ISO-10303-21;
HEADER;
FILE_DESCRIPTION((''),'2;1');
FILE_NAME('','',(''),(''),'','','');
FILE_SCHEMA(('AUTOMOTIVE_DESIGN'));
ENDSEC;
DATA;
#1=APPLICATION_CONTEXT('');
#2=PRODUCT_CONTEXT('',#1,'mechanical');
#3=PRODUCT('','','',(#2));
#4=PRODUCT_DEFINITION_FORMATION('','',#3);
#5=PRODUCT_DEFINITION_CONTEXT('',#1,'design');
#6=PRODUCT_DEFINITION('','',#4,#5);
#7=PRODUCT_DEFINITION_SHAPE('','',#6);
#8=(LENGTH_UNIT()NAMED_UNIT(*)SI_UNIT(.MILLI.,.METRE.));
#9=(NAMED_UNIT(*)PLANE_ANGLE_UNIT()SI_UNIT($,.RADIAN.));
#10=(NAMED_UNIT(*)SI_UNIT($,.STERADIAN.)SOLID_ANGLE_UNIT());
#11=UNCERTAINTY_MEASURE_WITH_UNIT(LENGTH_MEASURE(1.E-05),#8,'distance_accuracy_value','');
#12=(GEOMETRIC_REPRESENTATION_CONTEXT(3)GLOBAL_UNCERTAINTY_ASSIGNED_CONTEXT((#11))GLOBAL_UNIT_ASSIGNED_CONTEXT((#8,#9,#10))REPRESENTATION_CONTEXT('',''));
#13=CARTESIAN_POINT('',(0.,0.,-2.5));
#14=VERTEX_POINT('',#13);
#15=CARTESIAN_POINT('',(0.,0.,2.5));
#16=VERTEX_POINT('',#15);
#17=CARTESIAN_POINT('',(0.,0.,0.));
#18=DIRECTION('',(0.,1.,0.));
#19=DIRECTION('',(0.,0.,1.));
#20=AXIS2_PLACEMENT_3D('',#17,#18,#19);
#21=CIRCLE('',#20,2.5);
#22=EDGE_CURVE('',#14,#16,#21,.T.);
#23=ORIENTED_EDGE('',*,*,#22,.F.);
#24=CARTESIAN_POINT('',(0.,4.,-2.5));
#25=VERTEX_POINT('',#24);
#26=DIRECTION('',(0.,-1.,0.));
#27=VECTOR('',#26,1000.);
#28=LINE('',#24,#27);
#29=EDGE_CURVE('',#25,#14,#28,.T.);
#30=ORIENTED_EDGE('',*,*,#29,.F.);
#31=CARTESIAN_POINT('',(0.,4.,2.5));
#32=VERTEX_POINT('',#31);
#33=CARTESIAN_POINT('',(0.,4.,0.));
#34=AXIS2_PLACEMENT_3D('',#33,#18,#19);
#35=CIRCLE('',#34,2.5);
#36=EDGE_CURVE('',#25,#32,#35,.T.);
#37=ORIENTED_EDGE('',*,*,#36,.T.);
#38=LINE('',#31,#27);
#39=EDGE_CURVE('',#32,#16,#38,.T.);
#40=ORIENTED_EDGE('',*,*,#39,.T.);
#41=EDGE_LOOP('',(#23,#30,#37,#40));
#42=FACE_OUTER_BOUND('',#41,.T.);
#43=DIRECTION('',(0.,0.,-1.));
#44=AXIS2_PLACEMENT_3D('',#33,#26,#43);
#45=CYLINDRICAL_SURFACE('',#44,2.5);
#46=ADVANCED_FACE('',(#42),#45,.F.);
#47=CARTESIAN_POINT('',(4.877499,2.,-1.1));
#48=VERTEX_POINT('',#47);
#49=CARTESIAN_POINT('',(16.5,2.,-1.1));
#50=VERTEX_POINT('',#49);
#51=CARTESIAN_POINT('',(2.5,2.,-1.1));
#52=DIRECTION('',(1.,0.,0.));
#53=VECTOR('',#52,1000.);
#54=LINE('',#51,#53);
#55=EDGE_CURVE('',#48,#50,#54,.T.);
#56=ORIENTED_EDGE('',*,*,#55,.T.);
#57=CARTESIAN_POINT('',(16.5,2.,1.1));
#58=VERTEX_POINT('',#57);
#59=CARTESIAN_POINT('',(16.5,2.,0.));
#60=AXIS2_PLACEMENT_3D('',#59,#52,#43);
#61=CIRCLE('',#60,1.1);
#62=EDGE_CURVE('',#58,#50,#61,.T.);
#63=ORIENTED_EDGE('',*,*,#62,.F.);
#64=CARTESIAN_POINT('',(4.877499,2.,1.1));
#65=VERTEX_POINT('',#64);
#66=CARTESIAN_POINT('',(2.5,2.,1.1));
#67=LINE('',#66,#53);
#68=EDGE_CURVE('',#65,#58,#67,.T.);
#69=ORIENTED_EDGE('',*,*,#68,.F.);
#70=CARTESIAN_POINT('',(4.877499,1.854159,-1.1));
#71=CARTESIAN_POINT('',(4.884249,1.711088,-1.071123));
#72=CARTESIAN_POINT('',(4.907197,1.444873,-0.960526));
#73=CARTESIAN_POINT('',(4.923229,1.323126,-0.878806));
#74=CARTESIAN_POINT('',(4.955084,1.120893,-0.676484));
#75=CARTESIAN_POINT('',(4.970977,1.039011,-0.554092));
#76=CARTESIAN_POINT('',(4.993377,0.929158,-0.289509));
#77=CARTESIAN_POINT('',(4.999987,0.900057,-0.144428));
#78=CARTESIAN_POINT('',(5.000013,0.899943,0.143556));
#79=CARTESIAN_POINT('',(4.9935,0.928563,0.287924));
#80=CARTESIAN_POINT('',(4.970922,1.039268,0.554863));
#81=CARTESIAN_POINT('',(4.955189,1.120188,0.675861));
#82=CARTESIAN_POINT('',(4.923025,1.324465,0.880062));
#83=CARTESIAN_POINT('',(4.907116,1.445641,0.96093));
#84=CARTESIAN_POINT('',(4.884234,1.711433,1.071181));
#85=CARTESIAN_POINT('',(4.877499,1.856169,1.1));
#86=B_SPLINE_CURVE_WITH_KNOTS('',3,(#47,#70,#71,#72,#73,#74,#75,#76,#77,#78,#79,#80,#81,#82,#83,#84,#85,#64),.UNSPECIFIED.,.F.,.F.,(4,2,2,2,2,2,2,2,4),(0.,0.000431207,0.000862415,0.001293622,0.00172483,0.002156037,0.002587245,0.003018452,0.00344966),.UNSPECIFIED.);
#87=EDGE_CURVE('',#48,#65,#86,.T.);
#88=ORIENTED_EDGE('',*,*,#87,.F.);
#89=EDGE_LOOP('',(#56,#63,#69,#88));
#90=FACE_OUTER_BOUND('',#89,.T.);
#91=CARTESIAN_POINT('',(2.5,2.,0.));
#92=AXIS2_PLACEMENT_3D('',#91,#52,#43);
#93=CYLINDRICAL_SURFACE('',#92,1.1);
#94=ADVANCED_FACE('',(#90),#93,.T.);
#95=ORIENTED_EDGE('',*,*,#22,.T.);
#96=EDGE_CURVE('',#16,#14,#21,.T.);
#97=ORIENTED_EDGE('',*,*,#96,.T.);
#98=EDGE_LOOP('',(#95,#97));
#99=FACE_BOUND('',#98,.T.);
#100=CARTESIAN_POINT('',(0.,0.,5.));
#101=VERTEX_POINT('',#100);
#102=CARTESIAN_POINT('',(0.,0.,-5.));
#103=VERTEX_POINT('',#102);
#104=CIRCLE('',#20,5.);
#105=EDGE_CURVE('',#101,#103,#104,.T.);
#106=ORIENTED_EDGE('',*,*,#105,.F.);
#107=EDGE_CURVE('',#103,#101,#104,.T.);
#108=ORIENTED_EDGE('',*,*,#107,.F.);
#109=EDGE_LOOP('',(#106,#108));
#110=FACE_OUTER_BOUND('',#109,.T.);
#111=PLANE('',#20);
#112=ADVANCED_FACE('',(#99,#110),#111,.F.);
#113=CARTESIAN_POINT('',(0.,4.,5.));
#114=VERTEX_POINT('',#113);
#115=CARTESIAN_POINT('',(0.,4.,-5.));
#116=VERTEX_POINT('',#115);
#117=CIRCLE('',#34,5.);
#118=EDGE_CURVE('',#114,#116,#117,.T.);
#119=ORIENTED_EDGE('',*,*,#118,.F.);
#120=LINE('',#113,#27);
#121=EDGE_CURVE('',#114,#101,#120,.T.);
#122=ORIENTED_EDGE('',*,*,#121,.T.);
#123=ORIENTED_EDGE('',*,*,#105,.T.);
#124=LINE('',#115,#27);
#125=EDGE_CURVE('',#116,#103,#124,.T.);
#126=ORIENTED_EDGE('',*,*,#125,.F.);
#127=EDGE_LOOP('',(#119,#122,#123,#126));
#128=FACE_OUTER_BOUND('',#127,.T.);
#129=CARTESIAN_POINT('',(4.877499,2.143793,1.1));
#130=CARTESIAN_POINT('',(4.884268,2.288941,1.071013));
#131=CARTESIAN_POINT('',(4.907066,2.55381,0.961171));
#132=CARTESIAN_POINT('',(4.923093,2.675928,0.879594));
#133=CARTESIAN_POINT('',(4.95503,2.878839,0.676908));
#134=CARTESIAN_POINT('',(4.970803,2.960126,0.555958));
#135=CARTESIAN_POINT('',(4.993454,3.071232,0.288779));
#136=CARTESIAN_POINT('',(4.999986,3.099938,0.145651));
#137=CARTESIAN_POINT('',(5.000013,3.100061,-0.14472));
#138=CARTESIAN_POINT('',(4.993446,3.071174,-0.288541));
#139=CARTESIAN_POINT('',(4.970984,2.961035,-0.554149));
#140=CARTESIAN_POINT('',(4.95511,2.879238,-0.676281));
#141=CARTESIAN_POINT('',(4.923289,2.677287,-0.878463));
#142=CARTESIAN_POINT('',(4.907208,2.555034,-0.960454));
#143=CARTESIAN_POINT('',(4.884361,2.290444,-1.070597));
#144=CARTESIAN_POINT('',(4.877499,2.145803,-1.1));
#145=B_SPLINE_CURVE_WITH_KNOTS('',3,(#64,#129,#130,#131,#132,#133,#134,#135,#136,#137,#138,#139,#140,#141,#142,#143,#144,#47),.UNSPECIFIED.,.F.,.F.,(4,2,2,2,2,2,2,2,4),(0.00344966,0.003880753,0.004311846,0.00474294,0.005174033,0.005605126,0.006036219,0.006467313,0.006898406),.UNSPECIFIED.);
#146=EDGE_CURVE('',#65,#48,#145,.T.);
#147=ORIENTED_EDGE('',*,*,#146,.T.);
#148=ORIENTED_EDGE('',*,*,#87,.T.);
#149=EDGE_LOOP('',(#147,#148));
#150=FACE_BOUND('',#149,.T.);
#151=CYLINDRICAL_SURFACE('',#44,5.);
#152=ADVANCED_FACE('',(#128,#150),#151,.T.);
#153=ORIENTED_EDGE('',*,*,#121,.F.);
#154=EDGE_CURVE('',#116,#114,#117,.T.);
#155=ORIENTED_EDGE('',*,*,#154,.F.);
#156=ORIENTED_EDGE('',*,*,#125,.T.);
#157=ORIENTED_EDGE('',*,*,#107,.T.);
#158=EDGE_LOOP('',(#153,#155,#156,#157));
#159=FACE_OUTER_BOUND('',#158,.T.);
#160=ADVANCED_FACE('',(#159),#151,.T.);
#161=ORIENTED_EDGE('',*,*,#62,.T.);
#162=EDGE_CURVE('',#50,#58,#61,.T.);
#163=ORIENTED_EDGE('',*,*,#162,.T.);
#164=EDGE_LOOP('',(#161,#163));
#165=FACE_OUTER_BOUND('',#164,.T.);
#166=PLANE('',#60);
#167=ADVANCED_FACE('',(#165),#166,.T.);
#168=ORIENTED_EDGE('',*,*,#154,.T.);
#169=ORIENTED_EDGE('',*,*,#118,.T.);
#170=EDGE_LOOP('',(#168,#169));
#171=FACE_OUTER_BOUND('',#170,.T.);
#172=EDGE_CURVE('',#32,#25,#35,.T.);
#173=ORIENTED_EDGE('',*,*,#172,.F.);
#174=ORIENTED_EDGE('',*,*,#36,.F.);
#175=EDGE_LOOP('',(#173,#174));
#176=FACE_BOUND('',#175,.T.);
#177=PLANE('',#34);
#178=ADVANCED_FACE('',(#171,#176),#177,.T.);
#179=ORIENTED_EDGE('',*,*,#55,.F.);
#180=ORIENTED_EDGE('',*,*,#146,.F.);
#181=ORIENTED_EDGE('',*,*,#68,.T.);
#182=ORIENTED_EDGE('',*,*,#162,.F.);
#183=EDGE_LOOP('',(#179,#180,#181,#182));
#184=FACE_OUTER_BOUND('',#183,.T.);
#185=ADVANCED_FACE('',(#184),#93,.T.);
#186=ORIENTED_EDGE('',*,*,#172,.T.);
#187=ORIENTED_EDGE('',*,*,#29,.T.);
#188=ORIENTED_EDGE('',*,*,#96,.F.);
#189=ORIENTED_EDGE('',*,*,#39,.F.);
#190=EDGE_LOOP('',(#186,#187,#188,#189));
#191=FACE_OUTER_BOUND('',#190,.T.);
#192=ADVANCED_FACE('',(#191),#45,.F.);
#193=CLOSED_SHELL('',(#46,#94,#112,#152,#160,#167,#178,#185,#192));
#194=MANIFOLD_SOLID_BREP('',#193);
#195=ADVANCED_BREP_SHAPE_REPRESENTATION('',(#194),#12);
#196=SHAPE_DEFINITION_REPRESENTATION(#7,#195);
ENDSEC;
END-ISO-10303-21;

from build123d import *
from build123d.topology import SkipClean

# Parameters (mm, degrees)
HUB_RING_SKETCH_R    = 5
HUB_RING_SKETCH_R_2  = 2.5
HUB_RING_10X_5_DEPTH = 4
ARM_ROD_SKETCH_R     = 1.1
ARM_ROD_2_2_DEPTH    = 11.5
ARM_ROOT_SKETCH_R    = 1.1
ARM_ROOT_JOINT_DEPTH = 2.5


with BuildPart() as part:
    # Hub Ring Sketch → Hub Ring Ø10xØ5 (new body)
    with BuildSketch(Plane(origin=(0, 0, 0), x_dir=(1, 0, 0), z_dir=(0, 1, 0))):
        with Locations(Location((0, 0, 0), (0, 0, 270))):
            Circle(HUB_RING_SKETCH_R)
        with Locations(Location((0, 0, 0), (0, 0, 270))):
            Circle(HUB_RING_SKETCH_R_2, mode=Mode.SUBTRACT)
    extrude(amount=HUB_RING_10X_5_DEPTH)



with BuildPart() as body_2:
    # Arm Rod Sketch → Arm Rod Ø2.2 (new body)
    with BuildSketch(Plane(origin=(5, 0, 0), x_dir=(0, 0, -1), z_dir=(1, 0, 0))):
        with Locations((0, 2)):
            Circle(ARM_ROD_SKETCH_R)
    extrude(amount=ARM_ROD_2_2_DEPTH)


with BuildPart() as part_1:
    with SkipClean():  # the faces are left unmerged after this step: merging them gives an invalid solid
        add(part.part)

        add(body_2.part)  # Arm Root Joint merges body 2
        # Arm Root Sketch → Arm Root Joint (add)
        with BuildSketch(Plane(origin=(5, 0, 0), x_dir=(0, 0, -1), z_dir=(1, 0, 0))):
            with Locations((0, 2)):
                Circle(ARM_ROOT_SKETCH_R)
        extrude(amount=-ARM_ROOT_JOINT_DEPTH)


solid = part_1.part
